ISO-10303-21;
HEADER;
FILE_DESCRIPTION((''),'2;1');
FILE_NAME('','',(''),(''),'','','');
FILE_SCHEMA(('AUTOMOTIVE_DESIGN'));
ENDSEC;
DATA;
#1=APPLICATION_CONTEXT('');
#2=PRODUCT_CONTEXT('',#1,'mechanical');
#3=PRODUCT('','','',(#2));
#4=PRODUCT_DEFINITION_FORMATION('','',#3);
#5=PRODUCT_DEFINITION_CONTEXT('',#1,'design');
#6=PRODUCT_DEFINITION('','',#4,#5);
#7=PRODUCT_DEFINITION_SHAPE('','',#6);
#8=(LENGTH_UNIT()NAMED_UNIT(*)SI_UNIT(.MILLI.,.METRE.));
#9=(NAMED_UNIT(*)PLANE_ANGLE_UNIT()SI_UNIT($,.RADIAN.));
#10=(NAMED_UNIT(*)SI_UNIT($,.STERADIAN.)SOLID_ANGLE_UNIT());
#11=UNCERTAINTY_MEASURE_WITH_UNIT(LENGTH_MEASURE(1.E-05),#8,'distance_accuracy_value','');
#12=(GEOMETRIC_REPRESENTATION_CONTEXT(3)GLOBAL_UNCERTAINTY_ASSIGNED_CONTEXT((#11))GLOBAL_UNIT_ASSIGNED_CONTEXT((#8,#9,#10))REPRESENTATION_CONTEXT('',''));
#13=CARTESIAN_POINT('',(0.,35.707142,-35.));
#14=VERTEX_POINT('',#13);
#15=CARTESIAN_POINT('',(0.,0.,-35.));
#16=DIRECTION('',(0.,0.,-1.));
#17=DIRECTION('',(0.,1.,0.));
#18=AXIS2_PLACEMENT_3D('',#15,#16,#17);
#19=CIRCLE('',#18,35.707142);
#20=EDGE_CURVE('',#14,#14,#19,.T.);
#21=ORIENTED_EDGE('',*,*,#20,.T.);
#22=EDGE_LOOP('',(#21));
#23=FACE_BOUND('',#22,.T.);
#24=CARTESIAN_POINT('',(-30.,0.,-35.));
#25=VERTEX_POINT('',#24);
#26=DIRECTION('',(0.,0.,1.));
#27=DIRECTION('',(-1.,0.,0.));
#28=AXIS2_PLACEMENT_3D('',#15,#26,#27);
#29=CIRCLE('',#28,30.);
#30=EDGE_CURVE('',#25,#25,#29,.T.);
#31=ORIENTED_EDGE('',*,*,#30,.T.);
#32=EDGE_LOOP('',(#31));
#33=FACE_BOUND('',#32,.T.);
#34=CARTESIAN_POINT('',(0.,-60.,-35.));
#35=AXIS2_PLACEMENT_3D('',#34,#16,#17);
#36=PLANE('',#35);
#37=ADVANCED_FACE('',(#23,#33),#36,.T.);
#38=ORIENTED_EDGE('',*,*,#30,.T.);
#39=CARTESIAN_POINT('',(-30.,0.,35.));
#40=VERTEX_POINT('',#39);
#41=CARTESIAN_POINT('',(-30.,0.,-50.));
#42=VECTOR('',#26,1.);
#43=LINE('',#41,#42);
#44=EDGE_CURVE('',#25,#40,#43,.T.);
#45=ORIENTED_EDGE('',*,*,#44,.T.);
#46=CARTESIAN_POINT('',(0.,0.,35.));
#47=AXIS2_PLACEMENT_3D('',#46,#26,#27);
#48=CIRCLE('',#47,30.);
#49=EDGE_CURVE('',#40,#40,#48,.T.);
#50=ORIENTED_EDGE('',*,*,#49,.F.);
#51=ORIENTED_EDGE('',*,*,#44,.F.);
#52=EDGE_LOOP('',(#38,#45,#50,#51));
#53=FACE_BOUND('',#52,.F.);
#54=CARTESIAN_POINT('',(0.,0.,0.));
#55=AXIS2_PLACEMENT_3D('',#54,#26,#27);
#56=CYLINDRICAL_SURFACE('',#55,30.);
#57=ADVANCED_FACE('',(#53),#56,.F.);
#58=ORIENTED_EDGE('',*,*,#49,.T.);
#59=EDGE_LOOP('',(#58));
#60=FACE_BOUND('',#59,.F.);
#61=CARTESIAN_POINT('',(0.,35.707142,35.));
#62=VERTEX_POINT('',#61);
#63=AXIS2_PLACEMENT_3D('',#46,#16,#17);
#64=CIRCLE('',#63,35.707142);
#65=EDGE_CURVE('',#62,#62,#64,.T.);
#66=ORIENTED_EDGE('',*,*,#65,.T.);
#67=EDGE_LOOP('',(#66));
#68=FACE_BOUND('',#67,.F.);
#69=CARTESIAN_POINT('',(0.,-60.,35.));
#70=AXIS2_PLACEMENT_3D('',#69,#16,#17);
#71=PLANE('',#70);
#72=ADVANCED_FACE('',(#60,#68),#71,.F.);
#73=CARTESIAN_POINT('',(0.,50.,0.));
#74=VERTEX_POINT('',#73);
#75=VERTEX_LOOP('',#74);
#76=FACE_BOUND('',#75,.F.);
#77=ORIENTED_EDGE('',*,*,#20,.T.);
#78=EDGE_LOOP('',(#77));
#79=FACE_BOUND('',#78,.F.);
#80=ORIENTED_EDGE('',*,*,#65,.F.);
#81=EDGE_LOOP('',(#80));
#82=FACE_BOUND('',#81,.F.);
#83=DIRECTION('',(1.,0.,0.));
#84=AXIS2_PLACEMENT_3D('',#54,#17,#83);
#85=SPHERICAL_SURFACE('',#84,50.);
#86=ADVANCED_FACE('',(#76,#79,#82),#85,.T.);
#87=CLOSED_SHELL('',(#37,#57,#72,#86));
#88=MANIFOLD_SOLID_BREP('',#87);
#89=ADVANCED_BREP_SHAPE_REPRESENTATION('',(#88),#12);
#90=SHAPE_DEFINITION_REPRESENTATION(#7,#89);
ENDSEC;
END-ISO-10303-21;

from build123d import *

# Parameters (mm, degrees)
SKETCH_2_R           = 30
CUT_EXTRUDE_1_DEPTH  = 50
SKETCH_3_OUTSIDE_W   = 136.642
SKETCH_3_OUTSIDE_H   = 136.642
SKETCH_3_OUTSIDE_W_2 = 70
SKETCH_3_OUTSIDE_H_2 = 120
CUT_EXTRUDE_2_DEPTH  = 50


with BuildPart() as part:
    # 草图1 → 旋转1 (revolve)
    with BuildSketch(Plane.XY):
        with BuildLine():
            Line((0, 50), (0, -50))
            ThreePointArc((0, -50), (50, 0), (0, 50))
        make_face()
    revolve(axis=Axis((0, 50, 0), (0, -1, 0)))

    # 草图2 → 切除-拉伸1 (cut, symmetric)
    with BuildSketch(Plane.XY):
        with Locations(Location((0, 0, 0), (0, 0, 180))):
            Circle(SKETCH_2_R)
    extrude(amount=CUT_EXTRUDE_1_DEPTH, both=True, mode=Mode.SUBTRACT)

    # 草图3 outside → 切除-拉伸2 (cut, symmetric)
    with BuildSketch(Plane(origin=(0, 0, 0), x_dir=(0, 0, -1), z_dir=(1, 0, 0))):
        Rectangle(SKETCH_3_OUTSIDE_W, SKETCH_3_OUTSIDE_H)
        Rectangle(SKETCH_3_OUTSIDE_W_2, SKETCH_3_OUTSIDE_H_2, mode=Mode.SUBTRACT)
    extrude(amount=CUT_EXTRUDE_2_DEPTH, both=True, mode=Mode.SUBTRACT)


solid = part.part
